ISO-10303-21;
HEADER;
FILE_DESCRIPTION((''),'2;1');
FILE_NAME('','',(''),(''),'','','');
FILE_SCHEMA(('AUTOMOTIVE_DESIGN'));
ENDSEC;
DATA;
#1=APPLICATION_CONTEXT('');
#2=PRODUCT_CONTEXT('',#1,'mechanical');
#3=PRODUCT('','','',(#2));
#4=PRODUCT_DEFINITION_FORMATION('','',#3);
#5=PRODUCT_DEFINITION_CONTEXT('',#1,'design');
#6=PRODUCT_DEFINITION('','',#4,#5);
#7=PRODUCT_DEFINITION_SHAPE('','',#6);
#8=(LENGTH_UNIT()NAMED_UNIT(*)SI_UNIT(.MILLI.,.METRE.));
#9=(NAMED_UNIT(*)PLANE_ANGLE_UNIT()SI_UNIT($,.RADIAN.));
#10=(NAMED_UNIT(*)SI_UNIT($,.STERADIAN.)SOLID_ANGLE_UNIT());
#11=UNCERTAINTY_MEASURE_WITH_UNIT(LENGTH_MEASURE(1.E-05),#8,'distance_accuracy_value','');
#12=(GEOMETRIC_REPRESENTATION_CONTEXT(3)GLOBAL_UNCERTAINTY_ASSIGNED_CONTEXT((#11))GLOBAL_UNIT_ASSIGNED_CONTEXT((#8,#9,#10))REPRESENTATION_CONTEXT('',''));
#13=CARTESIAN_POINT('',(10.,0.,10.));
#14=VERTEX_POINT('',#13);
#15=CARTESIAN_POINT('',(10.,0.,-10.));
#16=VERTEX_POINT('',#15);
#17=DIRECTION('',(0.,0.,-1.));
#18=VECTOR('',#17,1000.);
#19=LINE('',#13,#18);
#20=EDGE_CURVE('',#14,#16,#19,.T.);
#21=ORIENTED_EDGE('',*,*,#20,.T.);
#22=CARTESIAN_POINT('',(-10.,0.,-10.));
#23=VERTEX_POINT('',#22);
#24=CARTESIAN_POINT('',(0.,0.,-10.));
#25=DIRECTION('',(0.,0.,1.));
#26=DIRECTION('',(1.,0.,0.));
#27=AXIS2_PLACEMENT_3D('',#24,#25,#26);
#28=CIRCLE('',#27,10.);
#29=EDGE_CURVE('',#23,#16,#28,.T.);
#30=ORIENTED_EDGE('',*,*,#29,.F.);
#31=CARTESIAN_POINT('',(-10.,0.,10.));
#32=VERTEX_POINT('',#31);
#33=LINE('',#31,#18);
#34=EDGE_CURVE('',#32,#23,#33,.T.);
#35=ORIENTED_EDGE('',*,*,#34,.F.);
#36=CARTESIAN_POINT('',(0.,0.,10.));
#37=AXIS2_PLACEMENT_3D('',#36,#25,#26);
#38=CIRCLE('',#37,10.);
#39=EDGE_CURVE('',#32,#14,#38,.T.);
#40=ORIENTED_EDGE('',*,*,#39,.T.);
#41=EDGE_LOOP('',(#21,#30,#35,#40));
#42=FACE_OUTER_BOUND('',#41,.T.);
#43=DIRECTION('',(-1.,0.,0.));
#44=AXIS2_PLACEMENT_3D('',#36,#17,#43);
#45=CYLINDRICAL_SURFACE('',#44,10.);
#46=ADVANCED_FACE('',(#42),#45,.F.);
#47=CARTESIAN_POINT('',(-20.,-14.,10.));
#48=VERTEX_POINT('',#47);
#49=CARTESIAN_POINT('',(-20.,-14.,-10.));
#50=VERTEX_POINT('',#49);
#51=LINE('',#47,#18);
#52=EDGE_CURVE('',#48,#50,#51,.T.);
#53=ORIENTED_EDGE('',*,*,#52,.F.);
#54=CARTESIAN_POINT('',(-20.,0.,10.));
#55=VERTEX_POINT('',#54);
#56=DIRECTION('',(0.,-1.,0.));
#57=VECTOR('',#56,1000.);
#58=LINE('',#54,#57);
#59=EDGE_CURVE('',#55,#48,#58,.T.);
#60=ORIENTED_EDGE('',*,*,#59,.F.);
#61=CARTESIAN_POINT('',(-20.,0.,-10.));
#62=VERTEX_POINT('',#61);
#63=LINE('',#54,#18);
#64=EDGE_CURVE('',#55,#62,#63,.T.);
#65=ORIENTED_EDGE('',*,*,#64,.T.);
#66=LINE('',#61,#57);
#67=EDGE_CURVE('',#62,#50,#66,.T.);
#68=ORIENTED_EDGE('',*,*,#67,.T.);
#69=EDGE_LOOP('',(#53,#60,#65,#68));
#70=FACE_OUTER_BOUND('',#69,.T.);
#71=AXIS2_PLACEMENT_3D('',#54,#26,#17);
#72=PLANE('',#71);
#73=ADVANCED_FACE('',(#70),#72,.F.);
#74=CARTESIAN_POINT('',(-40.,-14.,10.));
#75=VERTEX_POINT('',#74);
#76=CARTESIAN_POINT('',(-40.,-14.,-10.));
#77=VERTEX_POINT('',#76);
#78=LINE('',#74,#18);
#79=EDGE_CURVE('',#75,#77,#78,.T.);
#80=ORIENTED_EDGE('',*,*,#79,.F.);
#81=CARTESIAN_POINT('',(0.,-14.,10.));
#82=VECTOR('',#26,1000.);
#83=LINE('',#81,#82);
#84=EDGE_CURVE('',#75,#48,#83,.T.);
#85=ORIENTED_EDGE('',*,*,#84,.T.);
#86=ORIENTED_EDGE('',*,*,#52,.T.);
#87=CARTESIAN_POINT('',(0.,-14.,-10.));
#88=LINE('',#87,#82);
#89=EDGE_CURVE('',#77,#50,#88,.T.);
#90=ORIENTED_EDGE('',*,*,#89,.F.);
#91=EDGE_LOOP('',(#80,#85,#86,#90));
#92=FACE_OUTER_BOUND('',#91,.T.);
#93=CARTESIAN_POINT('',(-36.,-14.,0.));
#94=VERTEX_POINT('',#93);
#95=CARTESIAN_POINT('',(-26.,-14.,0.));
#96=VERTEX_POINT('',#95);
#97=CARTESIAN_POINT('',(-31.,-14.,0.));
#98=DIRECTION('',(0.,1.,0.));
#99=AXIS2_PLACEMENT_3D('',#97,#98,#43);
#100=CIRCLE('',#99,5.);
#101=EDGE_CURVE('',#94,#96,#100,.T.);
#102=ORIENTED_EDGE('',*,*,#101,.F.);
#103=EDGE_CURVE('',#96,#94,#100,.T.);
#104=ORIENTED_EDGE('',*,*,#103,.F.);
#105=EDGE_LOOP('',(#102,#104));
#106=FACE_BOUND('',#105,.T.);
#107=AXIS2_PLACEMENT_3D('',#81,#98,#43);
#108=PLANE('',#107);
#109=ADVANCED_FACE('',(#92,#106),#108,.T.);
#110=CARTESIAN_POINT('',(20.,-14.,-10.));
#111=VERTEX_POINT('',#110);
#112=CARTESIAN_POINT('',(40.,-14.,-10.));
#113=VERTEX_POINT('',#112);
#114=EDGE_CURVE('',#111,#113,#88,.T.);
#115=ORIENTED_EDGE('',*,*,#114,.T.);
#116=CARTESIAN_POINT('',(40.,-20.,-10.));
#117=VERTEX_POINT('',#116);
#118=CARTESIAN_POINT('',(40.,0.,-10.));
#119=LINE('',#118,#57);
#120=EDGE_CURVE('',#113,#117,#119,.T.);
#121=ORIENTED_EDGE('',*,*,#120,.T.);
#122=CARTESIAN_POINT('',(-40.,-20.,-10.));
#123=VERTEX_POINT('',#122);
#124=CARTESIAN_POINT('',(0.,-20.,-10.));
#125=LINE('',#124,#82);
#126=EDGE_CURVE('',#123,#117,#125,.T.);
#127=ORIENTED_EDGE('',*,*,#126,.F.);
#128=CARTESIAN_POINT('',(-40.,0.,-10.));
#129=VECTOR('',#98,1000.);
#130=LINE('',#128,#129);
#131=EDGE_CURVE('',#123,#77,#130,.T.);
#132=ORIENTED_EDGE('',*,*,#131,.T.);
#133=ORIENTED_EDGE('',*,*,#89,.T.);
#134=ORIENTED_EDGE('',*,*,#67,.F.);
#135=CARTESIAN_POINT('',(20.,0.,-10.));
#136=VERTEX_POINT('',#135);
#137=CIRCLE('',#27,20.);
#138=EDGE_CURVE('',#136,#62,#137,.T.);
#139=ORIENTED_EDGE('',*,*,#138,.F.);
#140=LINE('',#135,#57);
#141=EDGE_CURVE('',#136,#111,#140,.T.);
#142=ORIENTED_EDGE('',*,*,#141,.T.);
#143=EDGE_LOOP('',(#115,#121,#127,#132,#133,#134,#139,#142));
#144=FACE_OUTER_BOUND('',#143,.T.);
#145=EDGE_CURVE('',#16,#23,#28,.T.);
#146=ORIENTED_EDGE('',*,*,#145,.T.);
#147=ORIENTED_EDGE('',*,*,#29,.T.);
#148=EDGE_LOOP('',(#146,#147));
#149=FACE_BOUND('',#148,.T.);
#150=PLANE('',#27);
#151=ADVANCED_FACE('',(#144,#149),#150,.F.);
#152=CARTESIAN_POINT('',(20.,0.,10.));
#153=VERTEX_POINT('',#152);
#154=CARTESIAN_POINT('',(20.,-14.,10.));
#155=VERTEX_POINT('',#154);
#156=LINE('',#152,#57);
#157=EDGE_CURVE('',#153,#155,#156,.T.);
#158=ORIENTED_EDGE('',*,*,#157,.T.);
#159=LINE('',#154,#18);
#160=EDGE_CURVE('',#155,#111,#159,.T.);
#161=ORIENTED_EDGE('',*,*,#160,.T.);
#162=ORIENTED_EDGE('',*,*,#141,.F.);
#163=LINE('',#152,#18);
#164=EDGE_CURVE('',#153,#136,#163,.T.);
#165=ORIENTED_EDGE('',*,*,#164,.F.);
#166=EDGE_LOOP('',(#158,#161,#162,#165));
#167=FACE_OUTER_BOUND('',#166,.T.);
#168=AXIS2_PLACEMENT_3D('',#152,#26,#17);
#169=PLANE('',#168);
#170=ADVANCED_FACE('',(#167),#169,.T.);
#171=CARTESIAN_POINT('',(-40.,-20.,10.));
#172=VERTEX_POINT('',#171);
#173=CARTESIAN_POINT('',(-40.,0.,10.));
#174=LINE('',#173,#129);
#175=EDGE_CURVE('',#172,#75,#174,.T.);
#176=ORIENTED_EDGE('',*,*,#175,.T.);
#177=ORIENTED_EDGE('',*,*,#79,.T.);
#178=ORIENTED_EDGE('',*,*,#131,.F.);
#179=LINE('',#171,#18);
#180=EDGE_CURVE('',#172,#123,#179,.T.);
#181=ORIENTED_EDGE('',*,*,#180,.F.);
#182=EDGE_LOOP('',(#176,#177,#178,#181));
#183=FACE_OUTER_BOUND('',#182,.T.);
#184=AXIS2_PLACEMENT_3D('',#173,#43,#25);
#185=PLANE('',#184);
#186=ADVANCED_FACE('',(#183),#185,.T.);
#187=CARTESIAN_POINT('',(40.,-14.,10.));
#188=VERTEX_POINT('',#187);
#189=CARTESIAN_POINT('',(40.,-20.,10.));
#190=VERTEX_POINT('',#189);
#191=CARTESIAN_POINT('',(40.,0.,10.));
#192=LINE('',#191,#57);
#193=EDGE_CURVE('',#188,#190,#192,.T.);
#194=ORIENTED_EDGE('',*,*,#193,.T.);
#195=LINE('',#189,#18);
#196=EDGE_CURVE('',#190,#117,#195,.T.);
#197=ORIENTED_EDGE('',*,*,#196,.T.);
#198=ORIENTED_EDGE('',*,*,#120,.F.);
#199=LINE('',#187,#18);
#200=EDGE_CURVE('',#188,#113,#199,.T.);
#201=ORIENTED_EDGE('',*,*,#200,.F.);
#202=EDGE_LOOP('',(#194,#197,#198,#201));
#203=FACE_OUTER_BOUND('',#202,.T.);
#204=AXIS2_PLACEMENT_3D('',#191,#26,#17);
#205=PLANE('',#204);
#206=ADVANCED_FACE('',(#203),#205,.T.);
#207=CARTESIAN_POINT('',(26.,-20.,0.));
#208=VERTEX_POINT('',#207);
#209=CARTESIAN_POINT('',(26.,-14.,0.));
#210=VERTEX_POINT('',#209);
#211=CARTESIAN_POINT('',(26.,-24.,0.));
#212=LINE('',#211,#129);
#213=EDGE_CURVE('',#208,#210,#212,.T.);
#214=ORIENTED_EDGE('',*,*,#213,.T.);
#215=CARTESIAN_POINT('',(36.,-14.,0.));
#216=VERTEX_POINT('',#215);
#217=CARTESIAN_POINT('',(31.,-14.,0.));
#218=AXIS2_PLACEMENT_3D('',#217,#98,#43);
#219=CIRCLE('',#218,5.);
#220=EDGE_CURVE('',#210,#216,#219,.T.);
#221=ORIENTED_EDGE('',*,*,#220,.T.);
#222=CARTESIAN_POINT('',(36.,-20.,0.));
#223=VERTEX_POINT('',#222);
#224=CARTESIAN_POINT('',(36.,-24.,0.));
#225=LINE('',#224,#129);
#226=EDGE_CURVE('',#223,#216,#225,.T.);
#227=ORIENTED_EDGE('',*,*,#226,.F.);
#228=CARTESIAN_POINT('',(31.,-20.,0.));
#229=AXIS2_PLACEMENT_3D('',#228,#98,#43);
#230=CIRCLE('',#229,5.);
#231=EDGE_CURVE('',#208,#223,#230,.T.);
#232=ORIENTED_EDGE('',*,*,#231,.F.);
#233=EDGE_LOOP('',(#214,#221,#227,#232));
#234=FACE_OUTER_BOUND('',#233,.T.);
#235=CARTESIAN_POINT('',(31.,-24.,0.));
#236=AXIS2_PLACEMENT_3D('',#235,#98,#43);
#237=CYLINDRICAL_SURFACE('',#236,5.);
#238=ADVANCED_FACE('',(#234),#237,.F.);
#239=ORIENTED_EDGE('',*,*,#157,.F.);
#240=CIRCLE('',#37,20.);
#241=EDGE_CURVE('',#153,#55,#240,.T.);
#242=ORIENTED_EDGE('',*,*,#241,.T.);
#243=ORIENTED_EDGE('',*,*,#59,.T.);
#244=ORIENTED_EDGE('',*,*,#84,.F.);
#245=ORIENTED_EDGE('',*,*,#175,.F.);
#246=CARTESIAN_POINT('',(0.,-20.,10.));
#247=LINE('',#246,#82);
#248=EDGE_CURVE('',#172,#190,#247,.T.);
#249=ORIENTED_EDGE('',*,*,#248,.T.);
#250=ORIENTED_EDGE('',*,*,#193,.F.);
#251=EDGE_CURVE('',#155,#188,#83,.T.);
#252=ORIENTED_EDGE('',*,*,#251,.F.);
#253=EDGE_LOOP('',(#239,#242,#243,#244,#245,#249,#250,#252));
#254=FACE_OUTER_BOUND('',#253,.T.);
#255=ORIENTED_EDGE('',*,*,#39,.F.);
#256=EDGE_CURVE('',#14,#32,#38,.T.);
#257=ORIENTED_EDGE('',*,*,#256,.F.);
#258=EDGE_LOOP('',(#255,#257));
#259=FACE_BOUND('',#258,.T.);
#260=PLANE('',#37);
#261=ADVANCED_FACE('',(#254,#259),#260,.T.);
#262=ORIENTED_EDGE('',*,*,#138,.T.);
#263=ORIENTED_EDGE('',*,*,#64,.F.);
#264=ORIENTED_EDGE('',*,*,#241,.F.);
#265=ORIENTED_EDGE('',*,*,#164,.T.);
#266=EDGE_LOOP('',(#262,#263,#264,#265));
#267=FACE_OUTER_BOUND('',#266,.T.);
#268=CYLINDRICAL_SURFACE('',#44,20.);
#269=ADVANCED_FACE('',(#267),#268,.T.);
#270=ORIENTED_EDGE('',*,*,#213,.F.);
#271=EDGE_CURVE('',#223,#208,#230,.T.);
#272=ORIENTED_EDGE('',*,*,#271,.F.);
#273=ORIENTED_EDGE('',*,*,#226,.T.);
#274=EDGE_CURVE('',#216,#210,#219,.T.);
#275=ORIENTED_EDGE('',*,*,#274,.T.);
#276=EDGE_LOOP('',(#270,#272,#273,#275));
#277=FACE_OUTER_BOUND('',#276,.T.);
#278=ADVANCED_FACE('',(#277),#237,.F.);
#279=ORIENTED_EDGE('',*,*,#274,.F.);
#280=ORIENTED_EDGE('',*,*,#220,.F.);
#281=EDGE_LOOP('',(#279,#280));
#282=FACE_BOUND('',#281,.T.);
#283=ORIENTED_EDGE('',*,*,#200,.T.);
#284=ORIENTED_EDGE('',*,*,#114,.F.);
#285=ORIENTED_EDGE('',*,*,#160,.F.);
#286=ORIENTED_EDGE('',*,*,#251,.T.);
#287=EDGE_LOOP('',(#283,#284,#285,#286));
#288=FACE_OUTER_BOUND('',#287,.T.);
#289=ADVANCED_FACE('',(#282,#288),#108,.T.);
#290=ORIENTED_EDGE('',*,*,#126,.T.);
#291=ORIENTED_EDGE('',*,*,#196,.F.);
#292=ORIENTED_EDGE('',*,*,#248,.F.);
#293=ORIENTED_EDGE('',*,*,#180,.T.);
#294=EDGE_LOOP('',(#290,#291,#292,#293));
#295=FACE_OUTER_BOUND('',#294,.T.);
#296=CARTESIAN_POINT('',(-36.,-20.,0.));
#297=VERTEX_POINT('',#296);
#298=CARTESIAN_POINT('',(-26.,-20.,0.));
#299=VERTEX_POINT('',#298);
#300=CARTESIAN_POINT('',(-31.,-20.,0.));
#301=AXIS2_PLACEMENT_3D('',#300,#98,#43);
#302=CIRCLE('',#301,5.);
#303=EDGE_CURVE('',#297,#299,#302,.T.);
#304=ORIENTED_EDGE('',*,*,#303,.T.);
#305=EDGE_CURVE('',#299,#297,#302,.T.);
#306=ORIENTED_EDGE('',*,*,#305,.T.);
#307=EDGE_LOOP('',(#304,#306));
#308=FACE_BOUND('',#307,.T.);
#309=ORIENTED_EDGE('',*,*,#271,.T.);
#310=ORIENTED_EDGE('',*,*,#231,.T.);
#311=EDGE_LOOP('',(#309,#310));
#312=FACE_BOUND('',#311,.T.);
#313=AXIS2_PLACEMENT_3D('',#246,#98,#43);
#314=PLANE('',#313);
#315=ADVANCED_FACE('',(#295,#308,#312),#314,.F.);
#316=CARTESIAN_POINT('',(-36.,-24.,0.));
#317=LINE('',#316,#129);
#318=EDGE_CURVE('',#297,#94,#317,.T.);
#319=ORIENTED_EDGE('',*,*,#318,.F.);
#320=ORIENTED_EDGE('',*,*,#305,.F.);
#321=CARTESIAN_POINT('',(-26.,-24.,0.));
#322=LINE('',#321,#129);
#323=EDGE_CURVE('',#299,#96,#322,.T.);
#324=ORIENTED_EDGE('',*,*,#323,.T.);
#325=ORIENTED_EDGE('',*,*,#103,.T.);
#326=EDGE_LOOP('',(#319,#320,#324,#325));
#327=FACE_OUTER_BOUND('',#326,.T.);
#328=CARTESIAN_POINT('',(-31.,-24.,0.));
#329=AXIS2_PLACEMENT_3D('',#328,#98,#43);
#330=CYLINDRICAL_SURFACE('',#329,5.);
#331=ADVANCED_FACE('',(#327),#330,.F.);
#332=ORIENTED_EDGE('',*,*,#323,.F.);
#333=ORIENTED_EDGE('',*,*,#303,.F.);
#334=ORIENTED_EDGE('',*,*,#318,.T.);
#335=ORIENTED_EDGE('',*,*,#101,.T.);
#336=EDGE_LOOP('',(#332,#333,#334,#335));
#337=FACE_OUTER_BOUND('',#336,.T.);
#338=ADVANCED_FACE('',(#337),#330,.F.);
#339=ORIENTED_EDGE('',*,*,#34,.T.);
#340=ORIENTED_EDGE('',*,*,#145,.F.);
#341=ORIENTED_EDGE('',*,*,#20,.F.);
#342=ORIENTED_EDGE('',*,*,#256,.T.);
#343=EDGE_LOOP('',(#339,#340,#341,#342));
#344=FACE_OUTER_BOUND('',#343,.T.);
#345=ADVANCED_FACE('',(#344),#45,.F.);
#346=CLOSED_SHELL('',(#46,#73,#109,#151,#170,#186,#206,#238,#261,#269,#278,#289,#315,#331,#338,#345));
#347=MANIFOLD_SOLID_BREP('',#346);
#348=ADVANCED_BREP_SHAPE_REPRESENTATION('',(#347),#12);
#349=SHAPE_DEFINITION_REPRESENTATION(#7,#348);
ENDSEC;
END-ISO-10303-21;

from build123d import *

# Parameters (mm, degrees)
SKETCH1_R           = 10
BOSS_EXTRUDE1_DEPTH = 10
SKETCH2_R           = 5
CUT_EXTRUDE1_DEPTH  = 10


with BuildPart() as part:
    # Sketch1 → Boss-Extrude1 (new, symmetric)
    with BuildSketch(Plane.XY):
        with BuildLine():
            Line((-40, -14), (-40, -20))
            Line((-40, -20), (40, -20))
            Line((40, -20), (40, -14))
            Line((40, -14), (20, -14))
            Line((20, -14), (20, 0))
            ThreePointArc((20, 0), (0, 20), (-20, 0))
            Line((-20, 0), (-20, -14))
            Line((-20, -14), (-40, -14))
        make_face()
        Circle(SKETCH1_R, mode=Mode.SUBTRACT)
    extrude(amount=BOSS_EXTRUDE1_DEPTH, both=True)

    # Sketch2 → Cut-Extrude1 (cut, symmetric)
    with BuildSketch(Plane(origin=(0, -14, 0), x_dir=(1, 0, 0), z_dir=(0, 1, 0))):
        with Locations(Location((31, 0, 0), (0, 0, 180))):
            Circle(SKETCH2_R)
        with Locations(Location((-31, 0, 0), (0, 0, 180))):
            Circle(SKETCH2_R)
    extrude(amount=CUT_EXTRUDE1_DEPTH, both=True, mode=Mode.SUBTRACT)


solid = part.part
